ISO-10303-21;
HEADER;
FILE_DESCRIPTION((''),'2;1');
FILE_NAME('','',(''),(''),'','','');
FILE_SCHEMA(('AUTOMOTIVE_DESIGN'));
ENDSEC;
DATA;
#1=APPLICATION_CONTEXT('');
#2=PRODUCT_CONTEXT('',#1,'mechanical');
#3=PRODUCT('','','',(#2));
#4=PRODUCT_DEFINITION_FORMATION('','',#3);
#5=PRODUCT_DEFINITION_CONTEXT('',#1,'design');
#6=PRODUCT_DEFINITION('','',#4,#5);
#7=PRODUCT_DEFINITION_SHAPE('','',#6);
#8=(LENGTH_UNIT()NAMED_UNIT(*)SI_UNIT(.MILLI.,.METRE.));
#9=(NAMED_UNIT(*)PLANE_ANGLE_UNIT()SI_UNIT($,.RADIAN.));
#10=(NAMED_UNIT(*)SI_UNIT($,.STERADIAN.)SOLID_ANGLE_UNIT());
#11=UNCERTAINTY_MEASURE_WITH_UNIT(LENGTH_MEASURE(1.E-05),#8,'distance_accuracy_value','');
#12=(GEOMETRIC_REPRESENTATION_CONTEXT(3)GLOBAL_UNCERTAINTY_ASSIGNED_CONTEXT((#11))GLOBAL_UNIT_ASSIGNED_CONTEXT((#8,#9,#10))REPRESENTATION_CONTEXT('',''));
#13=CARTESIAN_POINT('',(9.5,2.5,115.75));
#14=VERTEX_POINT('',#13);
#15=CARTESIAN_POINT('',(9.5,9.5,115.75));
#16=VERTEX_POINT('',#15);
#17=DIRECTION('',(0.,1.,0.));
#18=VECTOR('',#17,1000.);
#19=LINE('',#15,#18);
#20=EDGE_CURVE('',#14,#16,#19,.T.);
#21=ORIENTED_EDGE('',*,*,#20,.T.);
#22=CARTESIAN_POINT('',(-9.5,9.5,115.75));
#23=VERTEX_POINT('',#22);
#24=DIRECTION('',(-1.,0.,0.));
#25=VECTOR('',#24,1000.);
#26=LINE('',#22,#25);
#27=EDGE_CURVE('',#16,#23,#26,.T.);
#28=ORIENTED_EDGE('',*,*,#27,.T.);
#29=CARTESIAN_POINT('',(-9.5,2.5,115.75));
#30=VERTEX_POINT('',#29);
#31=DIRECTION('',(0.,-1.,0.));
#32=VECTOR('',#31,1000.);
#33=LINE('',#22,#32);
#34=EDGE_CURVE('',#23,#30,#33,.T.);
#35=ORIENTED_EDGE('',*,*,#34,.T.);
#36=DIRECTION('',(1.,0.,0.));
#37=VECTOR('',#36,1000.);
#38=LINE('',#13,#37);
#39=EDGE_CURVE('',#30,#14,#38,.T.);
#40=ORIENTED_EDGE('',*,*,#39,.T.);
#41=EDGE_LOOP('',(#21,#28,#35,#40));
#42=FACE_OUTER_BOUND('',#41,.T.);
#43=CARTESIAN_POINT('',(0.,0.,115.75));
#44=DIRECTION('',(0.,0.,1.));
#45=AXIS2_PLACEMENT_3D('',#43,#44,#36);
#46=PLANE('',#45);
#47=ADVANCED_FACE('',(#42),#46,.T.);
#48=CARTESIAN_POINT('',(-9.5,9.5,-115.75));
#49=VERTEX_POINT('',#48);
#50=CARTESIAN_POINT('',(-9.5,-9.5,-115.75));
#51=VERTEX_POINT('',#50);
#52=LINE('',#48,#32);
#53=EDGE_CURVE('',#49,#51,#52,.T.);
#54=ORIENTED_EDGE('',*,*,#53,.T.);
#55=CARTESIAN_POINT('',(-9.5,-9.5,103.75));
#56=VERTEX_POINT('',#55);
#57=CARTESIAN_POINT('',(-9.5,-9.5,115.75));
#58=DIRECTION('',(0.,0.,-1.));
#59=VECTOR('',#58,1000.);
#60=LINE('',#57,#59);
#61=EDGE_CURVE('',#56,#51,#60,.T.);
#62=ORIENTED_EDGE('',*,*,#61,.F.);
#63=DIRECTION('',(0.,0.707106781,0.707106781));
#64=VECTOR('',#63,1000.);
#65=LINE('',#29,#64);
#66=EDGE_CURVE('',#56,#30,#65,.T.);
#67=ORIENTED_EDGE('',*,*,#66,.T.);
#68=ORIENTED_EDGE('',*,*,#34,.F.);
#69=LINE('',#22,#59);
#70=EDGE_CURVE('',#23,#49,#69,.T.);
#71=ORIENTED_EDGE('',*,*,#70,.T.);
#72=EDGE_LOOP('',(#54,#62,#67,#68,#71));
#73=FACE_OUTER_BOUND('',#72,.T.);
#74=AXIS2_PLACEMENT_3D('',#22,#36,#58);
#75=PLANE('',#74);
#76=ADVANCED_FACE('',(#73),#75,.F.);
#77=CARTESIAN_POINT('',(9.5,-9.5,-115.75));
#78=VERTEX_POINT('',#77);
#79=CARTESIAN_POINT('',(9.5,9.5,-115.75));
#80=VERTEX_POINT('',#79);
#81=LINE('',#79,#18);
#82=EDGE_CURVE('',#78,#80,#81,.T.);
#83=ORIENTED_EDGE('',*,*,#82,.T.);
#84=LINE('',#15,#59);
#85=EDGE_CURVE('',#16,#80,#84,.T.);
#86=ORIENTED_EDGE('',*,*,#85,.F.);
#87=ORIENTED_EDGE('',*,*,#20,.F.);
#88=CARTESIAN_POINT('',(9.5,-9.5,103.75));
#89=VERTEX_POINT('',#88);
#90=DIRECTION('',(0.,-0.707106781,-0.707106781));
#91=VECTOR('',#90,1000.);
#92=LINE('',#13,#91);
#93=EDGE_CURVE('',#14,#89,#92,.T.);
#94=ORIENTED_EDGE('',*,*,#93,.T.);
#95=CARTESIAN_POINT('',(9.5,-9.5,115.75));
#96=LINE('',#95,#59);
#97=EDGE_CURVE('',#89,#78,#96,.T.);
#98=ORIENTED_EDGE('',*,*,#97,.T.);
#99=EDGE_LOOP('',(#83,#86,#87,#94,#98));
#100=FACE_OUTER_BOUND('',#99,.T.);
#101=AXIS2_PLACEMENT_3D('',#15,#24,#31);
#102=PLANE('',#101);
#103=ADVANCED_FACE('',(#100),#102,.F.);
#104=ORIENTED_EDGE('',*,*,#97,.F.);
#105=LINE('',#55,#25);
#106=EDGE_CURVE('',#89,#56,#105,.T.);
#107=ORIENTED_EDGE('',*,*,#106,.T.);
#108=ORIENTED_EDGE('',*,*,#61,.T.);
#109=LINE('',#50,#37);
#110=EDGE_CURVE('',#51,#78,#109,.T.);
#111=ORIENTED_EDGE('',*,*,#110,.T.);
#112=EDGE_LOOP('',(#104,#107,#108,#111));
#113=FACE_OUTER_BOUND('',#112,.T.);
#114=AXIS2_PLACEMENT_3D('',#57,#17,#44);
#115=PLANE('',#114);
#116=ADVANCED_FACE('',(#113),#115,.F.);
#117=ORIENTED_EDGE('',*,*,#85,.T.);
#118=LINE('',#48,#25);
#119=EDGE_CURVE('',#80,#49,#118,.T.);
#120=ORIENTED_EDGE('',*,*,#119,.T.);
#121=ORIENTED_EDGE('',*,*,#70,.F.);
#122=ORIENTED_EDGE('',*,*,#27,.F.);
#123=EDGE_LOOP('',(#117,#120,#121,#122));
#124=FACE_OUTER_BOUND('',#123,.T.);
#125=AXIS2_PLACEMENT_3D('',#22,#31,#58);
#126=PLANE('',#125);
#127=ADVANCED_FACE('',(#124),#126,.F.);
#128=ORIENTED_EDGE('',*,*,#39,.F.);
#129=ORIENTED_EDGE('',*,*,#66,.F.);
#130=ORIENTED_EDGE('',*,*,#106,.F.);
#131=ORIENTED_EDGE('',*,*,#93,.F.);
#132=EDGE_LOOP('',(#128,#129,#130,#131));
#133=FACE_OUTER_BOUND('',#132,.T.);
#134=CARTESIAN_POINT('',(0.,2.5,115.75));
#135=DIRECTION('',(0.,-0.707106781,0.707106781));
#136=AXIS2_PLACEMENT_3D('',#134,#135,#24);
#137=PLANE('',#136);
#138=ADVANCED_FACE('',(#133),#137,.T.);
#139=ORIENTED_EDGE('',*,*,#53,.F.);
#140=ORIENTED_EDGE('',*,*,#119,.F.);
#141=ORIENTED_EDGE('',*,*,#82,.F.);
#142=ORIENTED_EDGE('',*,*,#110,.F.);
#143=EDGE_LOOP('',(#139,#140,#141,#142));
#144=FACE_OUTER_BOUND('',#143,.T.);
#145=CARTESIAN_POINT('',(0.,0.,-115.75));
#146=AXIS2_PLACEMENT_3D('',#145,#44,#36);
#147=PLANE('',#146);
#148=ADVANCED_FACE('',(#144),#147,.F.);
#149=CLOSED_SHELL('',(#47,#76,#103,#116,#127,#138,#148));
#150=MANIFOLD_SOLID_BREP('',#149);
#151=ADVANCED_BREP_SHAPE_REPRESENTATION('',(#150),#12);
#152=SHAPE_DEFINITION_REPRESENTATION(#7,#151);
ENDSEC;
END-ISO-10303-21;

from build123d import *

# Parameters (mm, degrees)
SKETCH1_W           = 19
SKETCH1_H           = 19
BOSS_EXTRUDE1_DEPTH = 115.75
CHAMFER1_SIZE       = 12


with BuildPart() as part:
    # Sketch1 → Boss-Extrude1 (new, symmetric)
    with BuildSketch(Plane.XY):
        Rectangle(SKETCH1_W, SKETCH1_H)
    extrude(amount=BOSS_EXTRUDE1_DEPTH, both=True)

    # Chamfer1
    chamfer1_edges = [part.edges().sort_by_distance(p)[0] for p in [
        (0, -9.5, 115.75),
    ]]
    chamfer(chamfer1_edges, length=CHAMFER1_SIZE)


solid = part.part
